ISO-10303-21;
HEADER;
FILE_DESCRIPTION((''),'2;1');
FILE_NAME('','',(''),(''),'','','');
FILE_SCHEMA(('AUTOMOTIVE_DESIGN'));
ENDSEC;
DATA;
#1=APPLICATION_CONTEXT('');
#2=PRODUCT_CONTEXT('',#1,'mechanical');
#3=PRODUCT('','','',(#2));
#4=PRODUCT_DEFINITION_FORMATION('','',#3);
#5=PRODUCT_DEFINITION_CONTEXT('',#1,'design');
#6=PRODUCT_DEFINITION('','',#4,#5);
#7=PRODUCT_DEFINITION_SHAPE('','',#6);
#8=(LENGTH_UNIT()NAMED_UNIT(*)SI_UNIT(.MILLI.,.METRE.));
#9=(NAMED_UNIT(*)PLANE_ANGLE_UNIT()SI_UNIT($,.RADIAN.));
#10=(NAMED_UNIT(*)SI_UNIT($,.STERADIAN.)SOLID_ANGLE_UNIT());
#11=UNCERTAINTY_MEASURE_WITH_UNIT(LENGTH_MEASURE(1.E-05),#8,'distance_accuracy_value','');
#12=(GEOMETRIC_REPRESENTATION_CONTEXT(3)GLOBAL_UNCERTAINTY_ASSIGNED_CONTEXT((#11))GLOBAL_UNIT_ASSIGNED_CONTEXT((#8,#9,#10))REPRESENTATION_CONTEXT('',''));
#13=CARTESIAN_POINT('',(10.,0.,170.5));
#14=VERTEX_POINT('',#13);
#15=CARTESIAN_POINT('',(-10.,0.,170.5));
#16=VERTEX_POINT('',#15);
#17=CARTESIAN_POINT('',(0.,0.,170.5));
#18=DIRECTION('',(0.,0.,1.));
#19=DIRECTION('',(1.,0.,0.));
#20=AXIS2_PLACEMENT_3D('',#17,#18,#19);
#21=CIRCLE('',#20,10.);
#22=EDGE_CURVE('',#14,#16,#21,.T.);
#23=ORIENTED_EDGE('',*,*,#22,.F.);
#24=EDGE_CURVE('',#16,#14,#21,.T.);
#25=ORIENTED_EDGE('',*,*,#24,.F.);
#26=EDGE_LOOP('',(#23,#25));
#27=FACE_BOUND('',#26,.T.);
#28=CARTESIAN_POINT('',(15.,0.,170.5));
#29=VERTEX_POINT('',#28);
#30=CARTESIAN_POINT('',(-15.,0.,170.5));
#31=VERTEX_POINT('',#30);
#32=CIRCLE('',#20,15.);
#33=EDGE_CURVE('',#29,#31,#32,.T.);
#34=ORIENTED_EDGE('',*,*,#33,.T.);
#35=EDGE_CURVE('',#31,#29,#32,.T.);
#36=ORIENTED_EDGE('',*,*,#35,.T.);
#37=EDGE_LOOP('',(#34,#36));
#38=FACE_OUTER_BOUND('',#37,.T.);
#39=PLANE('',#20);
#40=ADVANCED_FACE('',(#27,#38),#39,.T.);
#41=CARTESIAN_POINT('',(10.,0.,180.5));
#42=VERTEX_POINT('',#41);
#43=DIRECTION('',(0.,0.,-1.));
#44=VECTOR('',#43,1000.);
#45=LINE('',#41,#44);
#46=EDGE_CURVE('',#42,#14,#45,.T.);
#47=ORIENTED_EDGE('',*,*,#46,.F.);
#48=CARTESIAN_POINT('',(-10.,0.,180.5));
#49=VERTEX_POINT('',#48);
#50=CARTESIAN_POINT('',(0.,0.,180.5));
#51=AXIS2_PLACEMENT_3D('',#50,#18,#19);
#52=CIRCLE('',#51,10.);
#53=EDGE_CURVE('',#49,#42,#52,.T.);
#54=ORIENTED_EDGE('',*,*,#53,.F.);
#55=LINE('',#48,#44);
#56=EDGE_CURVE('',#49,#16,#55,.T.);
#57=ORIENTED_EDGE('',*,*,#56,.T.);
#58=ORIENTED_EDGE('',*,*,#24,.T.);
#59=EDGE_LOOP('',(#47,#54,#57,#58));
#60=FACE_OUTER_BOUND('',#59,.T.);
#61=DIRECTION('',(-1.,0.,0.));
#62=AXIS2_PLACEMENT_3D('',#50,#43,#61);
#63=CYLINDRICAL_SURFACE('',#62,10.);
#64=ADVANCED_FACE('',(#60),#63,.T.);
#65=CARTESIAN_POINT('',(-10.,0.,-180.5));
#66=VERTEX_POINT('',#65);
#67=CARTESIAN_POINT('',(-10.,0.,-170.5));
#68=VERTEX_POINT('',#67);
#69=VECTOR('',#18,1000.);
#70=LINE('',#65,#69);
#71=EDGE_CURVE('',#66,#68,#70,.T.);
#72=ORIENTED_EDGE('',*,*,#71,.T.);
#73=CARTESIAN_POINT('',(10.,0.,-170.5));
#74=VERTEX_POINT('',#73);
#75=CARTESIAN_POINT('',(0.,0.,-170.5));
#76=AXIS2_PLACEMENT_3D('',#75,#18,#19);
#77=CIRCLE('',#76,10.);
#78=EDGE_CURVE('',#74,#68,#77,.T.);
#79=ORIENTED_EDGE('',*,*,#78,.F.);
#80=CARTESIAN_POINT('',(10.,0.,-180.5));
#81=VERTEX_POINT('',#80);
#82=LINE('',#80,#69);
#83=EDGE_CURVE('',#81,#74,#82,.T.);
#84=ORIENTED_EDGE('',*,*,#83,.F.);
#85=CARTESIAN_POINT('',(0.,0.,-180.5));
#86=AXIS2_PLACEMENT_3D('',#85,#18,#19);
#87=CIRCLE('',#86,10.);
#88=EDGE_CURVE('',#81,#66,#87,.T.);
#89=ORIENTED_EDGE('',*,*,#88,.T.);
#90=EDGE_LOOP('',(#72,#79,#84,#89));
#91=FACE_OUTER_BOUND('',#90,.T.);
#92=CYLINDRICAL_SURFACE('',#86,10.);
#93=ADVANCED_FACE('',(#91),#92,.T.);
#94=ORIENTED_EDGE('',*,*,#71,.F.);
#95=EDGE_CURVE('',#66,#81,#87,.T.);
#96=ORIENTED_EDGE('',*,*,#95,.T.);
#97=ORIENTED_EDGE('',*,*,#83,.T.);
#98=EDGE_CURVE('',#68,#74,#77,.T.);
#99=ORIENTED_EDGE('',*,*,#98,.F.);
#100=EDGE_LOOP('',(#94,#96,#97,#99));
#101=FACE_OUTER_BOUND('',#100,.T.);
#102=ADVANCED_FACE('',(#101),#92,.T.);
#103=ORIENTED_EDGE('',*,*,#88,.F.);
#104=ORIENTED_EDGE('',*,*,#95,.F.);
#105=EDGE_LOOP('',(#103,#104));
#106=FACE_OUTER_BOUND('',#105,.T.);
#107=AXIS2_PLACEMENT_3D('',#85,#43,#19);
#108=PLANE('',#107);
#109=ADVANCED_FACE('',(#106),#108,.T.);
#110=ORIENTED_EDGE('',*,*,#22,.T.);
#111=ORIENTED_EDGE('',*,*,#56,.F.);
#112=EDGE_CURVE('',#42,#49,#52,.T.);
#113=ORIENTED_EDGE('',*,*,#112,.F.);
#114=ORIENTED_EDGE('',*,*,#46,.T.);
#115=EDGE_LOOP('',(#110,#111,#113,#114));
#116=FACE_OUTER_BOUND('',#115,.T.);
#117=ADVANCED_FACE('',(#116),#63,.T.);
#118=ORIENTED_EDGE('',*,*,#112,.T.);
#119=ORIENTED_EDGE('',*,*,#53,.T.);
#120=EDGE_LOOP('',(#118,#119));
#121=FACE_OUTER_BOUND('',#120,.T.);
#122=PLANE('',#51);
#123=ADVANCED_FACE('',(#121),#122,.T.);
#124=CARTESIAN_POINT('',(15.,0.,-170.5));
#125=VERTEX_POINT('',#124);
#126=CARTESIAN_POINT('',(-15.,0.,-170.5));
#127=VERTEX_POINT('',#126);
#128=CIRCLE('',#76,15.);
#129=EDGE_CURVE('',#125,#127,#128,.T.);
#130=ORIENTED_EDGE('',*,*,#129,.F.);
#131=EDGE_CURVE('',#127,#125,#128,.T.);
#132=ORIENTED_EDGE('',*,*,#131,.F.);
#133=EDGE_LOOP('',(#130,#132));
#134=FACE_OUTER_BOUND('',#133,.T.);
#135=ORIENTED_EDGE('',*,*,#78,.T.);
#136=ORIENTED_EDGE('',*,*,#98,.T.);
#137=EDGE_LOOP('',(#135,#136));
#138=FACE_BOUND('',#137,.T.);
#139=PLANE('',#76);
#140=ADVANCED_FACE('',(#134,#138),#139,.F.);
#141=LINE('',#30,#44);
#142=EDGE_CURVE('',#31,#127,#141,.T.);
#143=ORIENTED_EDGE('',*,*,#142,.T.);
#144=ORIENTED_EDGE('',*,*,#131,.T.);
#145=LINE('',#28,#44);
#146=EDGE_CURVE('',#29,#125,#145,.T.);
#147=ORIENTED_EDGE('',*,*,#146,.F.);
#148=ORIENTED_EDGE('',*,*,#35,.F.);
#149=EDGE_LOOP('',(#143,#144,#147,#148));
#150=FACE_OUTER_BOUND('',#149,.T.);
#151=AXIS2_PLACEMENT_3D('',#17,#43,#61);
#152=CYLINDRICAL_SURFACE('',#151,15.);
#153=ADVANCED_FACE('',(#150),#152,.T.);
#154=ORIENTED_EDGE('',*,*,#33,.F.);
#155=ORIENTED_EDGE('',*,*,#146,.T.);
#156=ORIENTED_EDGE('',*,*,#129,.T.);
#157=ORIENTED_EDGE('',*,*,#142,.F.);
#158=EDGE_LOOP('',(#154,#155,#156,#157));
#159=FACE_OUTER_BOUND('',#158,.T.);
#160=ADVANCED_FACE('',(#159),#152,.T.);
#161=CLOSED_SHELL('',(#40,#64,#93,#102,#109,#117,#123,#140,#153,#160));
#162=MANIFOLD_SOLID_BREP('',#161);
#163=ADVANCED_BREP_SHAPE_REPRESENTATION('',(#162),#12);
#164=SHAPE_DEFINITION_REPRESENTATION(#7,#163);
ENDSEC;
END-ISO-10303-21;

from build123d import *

# Parameters (mm, degrees)
SKETCH_1_R      = 15
EXTRUDE_1_DEPTH = 170.5
SKETCH_2_R      = 10
EXTRUDE_2_DEPTH = 10


with BuildPart() as part:
    # 草图1 → 凸台-拉伸1 (new, symmetric)
    with BuildSketch(Plane.XY):
        with Locations(Location((0, 0, 0), (0, 0, 180))):
            Circle(SKETCH_1_R)
    extrude(amount=EXTRUDE_1_DEPTH, both=True)

    # 草图2 → 凸台-拉伸2 (add)
    with BuildSketch(Plane.XY.offset(170.5)):
        Circle(SKETCH_2_R)
    extrude_2 = extrude(amount=EXTRUDE_2_DEPTH)

    # 镜向1: 凸台-拉伸2 across plane
    add(extrude_2.mirror(Plane.XY))


solid = part.part
